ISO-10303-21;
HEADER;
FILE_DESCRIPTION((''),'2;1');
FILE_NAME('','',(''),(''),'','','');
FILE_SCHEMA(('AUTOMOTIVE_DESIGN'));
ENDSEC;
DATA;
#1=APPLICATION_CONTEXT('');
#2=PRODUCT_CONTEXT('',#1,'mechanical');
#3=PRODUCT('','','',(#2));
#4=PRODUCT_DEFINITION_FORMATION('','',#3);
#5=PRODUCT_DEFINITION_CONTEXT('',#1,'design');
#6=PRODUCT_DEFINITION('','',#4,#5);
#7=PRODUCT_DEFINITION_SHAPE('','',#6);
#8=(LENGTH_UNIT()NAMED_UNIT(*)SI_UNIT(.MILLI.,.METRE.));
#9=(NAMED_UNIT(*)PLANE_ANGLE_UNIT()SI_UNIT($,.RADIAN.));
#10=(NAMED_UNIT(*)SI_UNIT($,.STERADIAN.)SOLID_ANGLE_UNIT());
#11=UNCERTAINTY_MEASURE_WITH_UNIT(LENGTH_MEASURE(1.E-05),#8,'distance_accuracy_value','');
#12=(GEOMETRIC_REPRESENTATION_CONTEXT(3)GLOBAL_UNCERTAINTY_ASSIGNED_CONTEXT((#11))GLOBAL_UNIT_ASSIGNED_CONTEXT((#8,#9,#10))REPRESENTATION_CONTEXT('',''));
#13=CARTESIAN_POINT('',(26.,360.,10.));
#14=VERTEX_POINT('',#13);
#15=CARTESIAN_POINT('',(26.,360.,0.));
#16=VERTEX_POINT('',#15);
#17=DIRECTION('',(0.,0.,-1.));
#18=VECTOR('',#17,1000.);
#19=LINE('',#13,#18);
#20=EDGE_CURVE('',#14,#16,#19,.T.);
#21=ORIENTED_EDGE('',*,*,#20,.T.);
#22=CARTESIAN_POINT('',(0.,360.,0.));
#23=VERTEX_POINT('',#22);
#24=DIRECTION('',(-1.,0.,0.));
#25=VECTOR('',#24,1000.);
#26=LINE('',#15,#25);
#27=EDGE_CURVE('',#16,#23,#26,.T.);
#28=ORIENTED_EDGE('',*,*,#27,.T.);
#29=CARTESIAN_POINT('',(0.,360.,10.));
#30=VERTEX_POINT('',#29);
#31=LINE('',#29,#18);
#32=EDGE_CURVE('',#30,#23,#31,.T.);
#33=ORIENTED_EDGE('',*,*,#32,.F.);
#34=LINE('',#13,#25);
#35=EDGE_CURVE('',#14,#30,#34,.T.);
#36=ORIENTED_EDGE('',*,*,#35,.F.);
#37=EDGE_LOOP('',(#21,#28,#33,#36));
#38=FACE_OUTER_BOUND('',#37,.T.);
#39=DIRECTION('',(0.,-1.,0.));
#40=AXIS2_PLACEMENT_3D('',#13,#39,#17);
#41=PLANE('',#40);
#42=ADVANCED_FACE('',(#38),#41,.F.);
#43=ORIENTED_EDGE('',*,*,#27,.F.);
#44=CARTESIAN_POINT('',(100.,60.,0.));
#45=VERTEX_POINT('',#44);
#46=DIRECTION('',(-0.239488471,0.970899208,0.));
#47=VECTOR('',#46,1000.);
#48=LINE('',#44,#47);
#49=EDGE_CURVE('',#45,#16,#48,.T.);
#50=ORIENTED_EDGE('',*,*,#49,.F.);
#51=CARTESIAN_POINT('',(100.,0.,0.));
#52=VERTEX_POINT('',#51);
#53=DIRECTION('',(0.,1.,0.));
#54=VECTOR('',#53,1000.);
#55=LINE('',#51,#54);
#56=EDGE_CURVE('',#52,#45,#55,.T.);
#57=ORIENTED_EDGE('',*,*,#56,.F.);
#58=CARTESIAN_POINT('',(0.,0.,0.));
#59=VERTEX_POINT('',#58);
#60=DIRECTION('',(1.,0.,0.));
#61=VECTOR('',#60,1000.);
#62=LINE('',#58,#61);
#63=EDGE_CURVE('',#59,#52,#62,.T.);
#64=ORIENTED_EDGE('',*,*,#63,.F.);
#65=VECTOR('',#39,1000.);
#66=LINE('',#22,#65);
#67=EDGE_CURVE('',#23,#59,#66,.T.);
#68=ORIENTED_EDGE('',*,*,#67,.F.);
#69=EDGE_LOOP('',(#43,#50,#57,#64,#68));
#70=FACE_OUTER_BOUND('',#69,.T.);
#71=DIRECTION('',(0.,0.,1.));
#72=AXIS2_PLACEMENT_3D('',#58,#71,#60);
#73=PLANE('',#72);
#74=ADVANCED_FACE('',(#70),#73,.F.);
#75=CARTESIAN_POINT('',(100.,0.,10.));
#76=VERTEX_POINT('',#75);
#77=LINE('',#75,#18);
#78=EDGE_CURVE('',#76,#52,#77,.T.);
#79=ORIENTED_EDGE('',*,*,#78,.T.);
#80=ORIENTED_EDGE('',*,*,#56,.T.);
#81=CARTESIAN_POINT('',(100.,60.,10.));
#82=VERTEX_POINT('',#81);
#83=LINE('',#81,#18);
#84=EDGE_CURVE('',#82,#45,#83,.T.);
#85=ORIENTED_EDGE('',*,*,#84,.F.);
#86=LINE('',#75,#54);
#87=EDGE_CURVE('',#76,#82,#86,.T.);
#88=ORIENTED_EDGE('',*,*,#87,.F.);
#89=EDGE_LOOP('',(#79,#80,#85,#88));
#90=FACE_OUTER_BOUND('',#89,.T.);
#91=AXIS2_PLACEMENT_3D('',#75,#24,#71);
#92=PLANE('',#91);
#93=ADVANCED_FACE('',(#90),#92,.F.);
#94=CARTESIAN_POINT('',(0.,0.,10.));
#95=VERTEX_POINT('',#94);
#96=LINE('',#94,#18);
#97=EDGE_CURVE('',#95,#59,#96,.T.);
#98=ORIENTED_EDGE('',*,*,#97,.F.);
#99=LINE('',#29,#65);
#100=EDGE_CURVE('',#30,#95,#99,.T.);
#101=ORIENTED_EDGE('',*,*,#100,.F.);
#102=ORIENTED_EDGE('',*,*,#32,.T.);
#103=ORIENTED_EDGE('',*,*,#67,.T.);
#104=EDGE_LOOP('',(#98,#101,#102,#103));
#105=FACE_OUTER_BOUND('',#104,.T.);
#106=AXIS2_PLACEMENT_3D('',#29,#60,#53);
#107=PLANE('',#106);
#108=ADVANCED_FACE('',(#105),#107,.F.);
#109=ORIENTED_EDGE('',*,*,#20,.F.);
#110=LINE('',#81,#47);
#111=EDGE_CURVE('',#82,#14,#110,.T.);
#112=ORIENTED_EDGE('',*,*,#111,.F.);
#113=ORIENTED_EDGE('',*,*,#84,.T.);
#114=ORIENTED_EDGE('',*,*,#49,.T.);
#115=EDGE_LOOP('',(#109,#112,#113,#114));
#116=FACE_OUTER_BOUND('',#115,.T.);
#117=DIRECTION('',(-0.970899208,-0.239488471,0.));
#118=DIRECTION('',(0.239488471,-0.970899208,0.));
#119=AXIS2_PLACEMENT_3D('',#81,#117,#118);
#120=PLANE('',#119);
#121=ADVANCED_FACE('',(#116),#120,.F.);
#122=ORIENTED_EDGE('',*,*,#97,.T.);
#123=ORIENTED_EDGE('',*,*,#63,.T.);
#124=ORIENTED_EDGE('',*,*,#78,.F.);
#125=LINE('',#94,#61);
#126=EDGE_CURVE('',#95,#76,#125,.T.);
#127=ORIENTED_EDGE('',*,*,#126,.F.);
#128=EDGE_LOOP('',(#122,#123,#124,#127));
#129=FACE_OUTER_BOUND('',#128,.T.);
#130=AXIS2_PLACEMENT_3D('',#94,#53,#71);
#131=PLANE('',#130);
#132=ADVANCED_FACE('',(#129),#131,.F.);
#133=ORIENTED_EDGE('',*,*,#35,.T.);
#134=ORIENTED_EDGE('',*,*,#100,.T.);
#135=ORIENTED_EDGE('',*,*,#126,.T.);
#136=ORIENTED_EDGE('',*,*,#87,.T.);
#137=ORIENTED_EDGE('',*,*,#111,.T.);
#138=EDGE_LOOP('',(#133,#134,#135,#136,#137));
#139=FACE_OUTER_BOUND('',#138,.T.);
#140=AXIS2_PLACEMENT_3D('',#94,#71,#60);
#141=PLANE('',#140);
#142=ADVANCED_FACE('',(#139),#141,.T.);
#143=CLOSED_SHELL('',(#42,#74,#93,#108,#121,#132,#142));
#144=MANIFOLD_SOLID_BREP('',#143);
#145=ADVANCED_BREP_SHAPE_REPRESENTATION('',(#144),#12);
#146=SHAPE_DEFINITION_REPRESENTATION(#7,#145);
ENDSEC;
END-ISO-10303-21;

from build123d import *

# Parameters (mm, degrees)
BOSS_EXTRUDE1_DEPTH = 10


with BuildPart() as part:
    # Sketch1 → Boss-Extrude1 (new body)
    with BuildSketch(Plane.XY):
        Polygon((0, 0), (100, 0), (100, 60), (26, 360), (0, 360), align=None)
    extrude(amount=BOSS_EXTRUDE1_DEPTH)


solid = part.part
